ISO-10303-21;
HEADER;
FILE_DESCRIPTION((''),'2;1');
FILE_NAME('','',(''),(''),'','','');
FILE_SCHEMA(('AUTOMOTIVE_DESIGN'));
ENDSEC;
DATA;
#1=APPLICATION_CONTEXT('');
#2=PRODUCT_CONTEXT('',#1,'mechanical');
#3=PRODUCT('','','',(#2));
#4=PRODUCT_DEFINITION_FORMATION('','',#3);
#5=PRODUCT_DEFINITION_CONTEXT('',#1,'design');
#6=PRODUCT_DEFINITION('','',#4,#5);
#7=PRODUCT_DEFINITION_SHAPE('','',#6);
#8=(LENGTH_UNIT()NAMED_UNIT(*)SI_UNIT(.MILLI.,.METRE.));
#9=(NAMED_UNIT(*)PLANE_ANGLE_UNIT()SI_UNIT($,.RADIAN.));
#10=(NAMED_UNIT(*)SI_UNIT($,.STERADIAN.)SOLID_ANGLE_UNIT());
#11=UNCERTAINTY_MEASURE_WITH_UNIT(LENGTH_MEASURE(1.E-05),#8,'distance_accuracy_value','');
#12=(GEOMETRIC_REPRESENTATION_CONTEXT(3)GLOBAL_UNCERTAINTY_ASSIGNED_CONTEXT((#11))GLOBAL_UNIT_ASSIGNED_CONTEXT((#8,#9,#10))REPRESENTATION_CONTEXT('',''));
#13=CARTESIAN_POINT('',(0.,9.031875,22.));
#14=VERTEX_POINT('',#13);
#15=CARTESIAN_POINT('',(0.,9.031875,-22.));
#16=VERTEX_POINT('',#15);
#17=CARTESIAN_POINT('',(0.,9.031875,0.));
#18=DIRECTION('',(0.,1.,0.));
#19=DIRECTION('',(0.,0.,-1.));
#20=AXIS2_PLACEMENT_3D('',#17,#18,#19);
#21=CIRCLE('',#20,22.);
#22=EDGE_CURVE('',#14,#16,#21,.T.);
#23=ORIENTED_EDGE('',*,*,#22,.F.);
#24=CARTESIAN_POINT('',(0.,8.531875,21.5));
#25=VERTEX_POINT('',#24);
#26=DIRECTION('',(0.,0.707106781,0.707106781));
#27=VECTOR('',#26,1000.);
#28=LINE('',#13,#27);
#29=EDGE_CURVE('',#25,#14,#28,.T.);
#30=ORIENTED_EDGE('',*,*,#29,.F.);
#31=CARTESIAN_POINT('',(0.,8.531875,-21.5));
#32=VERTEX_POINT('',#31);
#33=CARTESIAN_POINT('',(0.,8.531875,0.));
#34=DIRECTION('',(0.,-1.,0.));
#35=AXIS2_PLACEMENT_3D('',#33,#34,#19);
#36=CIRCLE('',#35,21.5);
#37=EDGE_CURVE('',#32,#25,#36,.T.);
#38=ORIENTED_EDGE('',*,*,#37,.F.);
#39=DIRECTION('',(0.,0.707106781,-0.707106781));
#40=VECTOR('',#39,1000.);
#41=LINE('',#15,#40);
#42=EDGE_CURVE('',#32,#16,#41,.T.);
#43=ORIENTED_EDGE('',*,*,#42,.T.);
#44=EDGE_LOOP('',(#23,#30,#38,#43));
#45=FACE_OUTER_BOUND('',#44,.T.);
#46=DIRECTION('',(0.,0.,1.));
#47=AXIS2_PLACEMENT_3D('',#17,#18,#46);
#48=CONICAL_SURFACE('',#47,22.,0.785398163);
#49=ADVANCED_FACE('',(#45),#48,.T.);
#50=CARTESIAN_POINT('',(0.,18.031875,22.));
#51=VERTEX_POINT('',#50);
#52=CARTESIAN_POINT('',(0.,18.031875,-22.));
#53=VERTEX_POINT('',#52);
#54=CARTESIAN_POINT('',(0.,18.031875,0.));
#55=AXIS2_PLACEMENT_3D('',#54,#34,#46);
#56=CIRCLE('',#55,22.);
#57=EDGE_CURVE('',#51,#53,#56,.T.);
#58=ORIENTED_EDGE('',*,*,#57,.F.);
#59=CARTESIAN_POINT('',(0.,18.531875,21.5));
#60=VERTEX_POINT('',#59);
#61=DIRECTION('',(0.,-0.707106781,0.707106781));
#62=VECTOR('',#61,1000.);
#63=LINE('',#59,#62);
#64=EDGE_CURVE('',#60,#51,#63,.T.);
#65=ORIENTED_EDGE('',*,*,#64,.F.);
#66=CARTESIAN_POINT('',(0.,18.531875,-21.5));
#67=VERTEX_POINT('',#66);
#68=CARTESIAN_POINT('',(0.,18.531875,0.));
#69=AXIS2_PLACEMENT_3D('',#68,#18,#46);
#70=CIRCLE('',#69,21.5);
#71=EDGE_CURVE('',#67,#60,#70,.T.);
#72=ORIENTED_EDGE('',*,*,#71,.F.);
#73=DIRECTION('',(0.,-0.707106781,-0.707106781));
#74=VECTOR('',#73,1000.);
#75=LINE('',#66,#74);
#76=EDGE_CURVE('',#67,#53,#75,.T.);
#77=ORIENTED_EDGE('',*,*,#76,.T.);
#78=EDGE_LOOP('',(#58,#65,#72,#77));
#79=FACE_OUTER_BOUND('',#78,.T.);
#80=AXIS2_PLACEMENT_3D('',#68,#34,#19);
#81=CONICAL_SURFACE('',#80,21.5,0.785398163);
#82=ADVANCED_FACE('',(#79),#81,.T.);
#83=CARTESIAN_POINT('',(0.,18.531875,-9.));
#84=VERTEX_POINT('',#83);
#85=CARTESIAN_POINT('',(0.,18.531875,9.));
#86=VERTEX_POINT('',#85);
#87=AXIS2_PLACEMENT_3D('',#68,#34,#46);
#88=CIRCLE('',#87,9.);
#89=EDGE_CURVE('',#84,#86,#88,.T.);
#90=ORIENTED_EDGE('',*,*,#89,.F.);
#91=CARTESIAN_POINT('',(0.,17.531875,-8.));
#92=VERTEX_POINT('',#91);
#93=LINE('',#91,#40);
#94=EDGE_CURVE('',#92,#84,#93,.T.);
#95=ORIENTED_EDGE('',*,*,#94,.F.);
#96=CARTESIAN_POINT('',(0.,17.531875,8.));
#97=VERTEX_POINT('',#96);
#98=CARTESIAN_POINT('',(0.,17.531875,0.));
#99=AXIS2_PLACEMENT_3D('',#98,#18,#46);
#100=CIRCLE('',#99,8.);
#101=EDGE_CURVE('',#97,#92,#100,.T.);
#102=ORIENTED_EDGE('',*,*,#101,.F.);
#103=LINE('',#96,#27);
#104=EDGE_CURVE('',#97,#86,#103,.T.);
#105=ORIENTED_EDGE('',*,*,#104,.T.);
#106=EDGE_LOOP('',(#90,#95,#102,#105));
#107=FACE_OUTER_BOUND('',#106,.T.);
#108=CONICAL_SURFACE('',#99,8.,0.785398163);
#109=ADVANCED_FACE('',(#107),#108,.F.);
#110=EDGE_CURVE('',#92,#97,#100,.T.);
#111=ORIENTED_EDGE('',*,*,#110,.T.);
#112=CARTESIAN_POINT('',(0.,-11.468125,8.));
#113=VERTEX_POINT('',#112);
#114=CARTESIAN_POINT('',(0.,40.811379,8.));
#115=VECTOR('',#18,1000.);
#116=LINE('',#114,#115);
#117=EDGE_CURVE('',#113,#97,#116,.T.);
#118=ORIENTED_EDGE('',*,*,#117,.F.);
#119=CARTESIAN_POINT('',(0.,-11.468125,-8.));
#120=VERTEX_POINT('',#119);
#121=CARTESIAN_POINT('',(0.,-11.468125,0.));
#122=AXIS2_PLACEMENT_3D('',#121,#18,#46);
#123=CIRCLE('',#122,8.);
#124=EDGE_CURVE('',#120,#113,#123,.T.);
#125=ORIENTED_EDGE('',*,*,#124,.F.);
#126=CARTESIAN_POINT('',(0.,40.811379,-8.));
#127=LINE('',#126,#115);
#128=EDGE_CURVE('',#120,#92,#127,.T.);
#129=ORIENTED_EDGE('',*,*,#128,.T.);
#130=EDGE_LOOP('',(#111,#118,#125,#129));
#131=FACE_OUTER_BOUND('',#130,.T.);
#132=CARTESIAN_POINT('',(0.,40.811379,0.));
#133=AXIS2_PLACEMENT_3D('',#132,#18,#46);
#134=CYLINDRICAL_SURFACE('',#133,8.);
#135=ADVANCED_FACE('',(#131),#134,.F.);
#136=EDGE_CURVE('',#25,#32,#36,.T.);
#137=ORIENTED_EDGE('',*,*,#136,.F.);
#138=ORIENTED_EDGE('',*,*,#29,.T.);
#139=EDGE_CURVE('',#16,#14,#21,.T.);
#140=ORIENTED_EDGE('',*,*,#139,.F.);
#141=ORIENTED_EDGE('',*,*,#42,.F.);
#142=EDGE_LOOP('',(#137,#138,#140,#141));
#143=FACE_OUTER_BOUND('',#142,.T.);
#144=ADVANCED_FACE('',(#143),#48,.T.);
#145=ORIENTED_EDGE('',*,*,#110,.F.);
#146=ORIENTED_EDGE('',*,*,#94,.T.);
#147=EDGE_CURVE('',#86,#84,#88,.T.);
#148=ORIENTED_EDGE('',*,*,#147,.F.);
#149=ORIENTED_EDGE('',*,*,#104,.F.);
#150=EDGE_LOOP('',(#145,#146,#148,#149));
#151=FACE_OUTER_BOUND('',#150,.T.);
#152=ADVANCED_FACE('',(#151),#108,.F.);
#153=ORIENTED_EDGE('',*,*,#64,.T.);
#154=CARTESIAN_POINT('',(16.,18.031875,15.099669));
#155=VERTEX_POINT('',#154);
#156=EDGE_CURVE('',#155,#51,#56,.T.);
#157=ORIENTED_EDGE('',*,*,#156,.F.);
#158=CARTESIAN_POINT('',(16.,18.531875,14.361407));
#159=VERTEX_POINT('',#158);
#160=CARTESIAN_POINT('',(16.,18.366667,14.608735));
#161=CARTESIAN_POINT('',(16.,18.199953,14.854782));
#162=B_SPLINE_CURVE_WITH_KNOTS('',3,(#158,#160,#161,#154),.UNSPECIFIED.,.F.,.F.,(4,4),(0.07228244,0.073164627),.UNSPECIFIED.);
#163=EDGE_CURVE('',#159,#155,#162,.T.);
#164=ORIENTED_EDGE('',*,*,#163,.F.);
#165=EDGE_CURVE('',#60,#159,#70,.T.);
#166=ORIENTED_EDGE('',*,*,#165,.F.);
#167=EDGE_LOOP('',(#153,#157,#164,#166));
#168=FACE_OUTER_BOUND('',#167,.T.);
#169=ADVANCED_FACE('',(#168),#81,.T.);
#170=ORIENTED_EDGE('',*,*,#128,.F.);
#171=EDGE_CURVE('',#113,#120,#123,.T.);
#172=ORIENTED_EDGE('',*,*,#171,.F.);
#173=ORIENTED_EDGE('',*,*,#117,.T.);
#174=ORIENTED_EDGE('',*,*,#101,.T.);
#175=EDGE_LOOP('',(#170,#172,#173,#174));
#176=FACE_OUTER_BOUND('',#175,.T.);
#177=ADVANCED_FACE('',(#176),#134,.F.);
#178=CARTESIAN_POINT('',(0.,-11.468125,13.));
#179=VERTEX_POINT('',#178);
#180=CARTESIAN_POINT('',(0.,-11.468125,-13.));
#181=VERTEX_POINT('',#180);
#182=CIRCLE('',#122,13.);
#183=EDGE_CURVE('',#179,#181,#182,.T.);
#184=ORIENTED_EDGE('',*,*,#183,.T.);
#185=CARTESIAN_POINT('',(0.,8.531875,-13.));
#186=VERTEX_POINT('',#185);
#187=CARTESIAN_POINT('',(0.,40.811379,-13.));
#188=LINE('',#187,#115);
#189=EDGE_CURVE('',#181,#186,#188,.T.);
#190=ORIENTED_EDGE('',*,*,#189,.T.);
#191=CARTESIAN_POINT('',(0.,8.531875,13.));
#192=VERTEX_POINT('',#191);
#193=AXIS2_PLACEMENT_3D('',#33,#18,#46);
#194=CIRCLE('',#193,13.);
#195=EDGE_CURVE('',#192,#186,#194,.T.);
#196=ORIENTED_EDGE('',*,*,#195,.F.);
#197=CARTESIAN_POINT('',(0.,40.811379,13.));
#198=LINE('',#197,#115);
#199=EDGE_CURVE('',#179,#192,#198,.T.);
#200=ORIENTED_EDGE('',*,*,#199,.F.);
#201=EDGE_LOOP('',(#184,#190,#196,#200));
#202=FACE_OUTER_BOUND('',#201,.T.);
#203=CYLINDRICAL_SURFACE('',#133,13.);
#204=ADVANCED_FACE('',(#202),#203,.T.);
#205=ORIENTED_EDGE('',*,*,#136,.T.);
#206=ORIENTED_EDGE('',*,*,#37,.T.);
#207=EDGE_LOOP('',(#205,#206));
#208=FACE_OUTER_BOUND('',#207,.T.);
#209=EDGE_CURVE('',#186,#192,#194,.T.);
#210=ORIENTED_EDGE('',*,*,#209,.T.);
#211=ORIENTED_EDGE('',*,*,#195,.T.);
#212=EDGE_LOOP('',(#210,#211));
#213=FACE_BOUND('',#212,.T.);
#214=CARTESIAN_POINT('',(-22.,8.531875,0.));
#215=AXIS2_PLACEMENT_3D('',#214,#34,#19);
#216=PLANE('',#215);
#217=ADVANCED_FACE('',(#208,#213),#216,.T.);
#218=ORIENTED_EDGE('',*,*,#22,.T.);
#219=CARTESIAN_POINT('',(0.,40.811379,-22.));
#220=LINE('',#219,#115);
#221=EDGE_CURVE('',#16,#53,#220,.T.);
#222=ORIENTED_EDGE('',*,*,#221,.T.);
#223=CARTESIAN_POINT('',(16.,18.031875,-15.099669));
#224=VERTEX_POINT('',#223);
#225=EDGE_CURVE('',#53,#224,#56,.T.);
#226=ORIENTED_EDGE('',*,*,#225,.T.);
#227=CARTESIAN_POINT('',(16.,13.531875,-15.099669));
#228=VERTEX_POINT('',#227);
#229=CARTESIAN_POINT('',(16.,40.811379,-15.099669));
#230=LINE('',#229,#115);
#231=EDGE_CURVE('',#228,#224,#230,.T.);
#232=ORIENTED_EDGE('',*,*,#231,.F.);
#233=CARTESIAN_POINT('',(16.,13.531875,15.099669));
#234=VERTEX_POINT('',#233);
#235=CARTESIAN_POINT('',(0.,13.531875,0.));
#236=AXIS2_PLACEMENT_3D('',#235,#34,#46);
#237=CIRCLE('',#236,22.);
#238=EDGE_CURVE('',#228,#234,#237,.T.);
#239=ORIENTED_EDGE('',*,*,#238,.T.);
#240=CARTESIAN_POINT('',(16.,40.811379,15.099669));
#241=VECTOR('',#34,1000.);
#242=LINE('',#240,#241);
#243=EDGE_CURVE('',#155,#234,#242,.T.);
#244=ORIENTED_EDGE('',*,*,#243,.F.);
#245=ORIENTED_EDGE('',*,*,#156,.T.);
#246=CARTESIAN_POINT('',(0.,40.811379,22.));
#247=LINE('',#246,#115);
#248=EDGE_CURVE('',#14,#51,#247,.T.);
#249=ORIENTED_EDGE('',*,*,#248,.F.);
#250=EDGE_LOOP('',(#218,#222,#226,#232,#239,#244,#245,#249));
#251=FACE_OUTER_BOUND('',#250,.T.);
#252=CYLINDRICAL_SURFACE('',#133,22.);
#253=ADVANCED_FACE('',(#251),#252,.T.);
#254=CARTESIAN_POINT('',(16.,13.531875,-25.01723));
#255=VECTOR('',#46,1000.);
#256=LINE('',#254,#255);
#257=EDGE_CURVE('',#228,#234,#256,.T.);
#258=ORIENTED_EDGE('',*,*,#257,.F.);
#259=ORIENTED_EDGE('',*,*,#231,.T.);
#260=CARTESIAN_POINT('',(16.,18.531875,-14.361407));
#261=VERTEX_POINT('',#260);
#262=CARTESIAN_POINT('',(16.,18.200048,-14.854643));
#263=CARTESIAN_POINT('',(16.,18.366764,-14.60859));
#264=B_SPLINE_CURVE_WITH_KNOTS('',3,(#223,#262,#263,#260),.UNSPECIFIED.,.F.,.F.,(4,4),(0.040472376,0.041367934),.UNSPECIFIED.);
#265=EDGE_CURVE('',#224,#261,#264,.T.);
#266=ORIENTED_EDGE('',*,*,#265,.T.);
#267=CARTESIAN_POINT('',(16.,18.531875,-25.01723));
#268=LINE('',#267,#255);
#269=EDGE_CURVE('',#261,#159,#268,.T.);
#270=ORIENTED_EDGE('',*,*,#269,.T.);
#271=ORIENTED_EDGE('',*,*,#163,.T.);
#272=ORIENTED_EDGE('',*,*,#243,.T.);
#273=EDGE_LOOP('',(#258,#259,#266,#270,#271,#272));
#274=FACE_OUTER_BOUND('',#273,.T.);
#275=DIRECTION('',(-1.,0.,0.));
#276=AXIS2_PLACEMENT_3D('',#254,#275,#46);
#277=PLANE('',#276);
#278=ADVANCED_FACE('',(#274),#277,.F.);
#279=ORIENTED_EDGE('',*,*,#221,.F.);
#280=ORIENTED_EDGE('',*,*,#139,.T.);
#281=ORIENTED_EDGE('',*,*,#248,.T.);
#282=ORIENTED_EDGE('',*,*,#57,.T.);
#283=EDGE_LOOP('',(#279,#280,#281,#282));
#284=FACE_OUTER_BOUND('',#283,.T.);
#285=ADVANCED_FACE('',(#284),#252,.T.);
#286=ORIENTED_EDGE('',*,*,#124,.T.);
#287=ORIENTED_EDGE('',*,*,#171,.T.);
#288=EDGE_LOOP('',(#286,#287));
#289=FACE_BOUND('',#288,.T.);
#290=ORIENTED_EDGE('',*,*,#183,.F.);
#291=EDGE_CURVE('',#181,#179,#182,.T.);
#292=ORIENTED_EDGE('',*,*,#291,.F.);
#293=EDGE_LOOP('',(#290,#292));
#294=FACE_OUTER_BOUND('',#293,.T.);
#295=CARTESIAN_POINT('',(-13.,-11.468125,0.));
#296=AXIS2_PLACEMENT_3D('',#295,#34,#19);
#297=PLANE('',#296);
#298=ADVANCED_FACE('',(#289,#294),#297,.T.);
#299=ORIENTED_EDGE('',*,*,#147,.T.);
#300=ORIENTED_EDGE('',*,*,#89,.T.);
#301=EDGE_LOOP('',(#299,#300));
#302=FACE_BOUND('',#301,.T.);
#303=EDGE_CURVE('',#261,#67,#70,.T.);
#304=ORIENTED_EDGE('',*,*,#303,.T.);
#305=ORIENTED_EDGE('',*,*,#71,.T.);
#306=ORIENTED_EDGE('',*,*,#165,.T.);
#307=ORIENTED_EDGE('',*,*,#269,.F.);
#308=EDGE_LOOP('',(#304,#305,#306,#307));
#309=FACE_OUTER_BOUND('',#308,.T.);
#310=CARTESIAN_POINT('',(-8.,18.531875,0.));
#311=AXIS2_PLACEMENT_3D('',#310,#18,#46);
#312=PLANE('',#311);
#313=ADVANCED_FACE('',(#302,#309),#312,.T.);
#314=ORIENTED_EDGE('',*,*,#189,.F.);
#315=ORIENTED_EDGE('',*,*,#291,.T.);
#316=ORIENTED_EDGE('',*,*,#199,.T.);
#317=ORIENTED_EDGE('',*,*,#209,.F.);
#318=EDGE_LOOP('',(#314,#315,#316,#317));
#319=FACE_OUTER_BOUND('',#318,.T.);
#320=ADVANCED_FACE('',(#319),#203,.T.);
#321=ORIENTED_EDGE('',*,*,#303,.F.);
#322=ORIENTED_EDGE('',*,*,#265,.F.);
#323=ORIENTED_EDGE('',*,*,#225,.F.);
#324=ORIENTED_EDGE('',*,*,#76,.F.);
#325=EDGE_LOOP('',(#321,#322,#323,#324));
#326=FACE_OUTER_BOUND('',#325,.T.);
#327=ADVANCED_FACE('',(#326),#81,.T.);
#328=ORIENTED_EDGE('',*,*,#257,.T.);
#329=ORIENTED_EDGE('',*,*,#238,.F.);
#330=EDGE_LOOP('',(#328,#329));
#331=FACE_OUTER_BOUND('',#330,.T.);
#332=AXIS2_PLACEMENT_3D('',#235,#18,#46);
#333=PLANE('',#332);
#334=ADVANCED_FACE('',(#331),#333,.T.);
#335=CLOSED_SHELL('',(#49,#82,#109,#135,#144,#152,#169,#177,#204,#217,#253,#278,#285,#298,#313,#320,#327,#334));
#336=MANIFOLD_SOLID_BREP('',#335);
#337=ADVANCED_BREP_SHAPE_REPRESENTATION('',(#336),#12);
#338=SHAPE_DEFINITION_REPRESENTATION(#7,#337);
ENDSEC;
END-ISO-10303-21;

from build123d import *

# Parameters (mm, degrees)
CHAMFER1_SIZE      = 0.5
CHAMFER2_SIZE      = 1
SKETCH2_W          = 20.223718868
SKETCH2_H          = 51.853895089
CUT_EXTRUDE1_DEPTH = 5


with BuildPart() as part:
    # Sketch1 → Revolve1 (revolve)
    with BuildSketch(Plane.XY, mode=Mode.PRIVATE) as revolve1_sk:
        Polygon((-22, 18.531875125), (-22, 8.531875125), (-13, 8.531875125), (-13, -11.468124875), (-8, -11.468124875), (-8, 18.531875125), align=None)
    revolve(revolve1_sk.sketch.rotate(Axis((0, 40.811378681, 0), (0, -1, 0)), 270), axis=Axis((0, 40.811378681, 0), (0, -1, 0)))

    # Chamfer1
    chamfer1_edges = [part.edges().sort_by_distance(p)[0] for p in [
        (0, 8.531875125, -22),
        (0, 18.531875125, -22),
    ]]
    chamfer(chamfer1_edges, length=CHAMFER1_SIZE)

    # Chamfer2
    chamfer2_edges = [part.edges().sort_by_distance(p)[0] for p in [
        (0, 18.531875125, -8),
    ]]
    chamfer(chamfer2_edges, length=CHAMFER2_SIZE)

    # Sketch2 → Cut-Extrude1 (cut)
    with BuildSketch(Plane(origin=(0, 18.531875125, 0), x_dir=(1, 0, 0), z_dir=(0, 1, 0))):
        with Locations((26.111859434, -0.909717457)):
            Rectangle(SKETCH2_W, SKETCH2_H)
    extrude(amount=-CUT_EXTRUDE1_DEPTH, mode=Mode.SUBTRACT)


solid = part.part
